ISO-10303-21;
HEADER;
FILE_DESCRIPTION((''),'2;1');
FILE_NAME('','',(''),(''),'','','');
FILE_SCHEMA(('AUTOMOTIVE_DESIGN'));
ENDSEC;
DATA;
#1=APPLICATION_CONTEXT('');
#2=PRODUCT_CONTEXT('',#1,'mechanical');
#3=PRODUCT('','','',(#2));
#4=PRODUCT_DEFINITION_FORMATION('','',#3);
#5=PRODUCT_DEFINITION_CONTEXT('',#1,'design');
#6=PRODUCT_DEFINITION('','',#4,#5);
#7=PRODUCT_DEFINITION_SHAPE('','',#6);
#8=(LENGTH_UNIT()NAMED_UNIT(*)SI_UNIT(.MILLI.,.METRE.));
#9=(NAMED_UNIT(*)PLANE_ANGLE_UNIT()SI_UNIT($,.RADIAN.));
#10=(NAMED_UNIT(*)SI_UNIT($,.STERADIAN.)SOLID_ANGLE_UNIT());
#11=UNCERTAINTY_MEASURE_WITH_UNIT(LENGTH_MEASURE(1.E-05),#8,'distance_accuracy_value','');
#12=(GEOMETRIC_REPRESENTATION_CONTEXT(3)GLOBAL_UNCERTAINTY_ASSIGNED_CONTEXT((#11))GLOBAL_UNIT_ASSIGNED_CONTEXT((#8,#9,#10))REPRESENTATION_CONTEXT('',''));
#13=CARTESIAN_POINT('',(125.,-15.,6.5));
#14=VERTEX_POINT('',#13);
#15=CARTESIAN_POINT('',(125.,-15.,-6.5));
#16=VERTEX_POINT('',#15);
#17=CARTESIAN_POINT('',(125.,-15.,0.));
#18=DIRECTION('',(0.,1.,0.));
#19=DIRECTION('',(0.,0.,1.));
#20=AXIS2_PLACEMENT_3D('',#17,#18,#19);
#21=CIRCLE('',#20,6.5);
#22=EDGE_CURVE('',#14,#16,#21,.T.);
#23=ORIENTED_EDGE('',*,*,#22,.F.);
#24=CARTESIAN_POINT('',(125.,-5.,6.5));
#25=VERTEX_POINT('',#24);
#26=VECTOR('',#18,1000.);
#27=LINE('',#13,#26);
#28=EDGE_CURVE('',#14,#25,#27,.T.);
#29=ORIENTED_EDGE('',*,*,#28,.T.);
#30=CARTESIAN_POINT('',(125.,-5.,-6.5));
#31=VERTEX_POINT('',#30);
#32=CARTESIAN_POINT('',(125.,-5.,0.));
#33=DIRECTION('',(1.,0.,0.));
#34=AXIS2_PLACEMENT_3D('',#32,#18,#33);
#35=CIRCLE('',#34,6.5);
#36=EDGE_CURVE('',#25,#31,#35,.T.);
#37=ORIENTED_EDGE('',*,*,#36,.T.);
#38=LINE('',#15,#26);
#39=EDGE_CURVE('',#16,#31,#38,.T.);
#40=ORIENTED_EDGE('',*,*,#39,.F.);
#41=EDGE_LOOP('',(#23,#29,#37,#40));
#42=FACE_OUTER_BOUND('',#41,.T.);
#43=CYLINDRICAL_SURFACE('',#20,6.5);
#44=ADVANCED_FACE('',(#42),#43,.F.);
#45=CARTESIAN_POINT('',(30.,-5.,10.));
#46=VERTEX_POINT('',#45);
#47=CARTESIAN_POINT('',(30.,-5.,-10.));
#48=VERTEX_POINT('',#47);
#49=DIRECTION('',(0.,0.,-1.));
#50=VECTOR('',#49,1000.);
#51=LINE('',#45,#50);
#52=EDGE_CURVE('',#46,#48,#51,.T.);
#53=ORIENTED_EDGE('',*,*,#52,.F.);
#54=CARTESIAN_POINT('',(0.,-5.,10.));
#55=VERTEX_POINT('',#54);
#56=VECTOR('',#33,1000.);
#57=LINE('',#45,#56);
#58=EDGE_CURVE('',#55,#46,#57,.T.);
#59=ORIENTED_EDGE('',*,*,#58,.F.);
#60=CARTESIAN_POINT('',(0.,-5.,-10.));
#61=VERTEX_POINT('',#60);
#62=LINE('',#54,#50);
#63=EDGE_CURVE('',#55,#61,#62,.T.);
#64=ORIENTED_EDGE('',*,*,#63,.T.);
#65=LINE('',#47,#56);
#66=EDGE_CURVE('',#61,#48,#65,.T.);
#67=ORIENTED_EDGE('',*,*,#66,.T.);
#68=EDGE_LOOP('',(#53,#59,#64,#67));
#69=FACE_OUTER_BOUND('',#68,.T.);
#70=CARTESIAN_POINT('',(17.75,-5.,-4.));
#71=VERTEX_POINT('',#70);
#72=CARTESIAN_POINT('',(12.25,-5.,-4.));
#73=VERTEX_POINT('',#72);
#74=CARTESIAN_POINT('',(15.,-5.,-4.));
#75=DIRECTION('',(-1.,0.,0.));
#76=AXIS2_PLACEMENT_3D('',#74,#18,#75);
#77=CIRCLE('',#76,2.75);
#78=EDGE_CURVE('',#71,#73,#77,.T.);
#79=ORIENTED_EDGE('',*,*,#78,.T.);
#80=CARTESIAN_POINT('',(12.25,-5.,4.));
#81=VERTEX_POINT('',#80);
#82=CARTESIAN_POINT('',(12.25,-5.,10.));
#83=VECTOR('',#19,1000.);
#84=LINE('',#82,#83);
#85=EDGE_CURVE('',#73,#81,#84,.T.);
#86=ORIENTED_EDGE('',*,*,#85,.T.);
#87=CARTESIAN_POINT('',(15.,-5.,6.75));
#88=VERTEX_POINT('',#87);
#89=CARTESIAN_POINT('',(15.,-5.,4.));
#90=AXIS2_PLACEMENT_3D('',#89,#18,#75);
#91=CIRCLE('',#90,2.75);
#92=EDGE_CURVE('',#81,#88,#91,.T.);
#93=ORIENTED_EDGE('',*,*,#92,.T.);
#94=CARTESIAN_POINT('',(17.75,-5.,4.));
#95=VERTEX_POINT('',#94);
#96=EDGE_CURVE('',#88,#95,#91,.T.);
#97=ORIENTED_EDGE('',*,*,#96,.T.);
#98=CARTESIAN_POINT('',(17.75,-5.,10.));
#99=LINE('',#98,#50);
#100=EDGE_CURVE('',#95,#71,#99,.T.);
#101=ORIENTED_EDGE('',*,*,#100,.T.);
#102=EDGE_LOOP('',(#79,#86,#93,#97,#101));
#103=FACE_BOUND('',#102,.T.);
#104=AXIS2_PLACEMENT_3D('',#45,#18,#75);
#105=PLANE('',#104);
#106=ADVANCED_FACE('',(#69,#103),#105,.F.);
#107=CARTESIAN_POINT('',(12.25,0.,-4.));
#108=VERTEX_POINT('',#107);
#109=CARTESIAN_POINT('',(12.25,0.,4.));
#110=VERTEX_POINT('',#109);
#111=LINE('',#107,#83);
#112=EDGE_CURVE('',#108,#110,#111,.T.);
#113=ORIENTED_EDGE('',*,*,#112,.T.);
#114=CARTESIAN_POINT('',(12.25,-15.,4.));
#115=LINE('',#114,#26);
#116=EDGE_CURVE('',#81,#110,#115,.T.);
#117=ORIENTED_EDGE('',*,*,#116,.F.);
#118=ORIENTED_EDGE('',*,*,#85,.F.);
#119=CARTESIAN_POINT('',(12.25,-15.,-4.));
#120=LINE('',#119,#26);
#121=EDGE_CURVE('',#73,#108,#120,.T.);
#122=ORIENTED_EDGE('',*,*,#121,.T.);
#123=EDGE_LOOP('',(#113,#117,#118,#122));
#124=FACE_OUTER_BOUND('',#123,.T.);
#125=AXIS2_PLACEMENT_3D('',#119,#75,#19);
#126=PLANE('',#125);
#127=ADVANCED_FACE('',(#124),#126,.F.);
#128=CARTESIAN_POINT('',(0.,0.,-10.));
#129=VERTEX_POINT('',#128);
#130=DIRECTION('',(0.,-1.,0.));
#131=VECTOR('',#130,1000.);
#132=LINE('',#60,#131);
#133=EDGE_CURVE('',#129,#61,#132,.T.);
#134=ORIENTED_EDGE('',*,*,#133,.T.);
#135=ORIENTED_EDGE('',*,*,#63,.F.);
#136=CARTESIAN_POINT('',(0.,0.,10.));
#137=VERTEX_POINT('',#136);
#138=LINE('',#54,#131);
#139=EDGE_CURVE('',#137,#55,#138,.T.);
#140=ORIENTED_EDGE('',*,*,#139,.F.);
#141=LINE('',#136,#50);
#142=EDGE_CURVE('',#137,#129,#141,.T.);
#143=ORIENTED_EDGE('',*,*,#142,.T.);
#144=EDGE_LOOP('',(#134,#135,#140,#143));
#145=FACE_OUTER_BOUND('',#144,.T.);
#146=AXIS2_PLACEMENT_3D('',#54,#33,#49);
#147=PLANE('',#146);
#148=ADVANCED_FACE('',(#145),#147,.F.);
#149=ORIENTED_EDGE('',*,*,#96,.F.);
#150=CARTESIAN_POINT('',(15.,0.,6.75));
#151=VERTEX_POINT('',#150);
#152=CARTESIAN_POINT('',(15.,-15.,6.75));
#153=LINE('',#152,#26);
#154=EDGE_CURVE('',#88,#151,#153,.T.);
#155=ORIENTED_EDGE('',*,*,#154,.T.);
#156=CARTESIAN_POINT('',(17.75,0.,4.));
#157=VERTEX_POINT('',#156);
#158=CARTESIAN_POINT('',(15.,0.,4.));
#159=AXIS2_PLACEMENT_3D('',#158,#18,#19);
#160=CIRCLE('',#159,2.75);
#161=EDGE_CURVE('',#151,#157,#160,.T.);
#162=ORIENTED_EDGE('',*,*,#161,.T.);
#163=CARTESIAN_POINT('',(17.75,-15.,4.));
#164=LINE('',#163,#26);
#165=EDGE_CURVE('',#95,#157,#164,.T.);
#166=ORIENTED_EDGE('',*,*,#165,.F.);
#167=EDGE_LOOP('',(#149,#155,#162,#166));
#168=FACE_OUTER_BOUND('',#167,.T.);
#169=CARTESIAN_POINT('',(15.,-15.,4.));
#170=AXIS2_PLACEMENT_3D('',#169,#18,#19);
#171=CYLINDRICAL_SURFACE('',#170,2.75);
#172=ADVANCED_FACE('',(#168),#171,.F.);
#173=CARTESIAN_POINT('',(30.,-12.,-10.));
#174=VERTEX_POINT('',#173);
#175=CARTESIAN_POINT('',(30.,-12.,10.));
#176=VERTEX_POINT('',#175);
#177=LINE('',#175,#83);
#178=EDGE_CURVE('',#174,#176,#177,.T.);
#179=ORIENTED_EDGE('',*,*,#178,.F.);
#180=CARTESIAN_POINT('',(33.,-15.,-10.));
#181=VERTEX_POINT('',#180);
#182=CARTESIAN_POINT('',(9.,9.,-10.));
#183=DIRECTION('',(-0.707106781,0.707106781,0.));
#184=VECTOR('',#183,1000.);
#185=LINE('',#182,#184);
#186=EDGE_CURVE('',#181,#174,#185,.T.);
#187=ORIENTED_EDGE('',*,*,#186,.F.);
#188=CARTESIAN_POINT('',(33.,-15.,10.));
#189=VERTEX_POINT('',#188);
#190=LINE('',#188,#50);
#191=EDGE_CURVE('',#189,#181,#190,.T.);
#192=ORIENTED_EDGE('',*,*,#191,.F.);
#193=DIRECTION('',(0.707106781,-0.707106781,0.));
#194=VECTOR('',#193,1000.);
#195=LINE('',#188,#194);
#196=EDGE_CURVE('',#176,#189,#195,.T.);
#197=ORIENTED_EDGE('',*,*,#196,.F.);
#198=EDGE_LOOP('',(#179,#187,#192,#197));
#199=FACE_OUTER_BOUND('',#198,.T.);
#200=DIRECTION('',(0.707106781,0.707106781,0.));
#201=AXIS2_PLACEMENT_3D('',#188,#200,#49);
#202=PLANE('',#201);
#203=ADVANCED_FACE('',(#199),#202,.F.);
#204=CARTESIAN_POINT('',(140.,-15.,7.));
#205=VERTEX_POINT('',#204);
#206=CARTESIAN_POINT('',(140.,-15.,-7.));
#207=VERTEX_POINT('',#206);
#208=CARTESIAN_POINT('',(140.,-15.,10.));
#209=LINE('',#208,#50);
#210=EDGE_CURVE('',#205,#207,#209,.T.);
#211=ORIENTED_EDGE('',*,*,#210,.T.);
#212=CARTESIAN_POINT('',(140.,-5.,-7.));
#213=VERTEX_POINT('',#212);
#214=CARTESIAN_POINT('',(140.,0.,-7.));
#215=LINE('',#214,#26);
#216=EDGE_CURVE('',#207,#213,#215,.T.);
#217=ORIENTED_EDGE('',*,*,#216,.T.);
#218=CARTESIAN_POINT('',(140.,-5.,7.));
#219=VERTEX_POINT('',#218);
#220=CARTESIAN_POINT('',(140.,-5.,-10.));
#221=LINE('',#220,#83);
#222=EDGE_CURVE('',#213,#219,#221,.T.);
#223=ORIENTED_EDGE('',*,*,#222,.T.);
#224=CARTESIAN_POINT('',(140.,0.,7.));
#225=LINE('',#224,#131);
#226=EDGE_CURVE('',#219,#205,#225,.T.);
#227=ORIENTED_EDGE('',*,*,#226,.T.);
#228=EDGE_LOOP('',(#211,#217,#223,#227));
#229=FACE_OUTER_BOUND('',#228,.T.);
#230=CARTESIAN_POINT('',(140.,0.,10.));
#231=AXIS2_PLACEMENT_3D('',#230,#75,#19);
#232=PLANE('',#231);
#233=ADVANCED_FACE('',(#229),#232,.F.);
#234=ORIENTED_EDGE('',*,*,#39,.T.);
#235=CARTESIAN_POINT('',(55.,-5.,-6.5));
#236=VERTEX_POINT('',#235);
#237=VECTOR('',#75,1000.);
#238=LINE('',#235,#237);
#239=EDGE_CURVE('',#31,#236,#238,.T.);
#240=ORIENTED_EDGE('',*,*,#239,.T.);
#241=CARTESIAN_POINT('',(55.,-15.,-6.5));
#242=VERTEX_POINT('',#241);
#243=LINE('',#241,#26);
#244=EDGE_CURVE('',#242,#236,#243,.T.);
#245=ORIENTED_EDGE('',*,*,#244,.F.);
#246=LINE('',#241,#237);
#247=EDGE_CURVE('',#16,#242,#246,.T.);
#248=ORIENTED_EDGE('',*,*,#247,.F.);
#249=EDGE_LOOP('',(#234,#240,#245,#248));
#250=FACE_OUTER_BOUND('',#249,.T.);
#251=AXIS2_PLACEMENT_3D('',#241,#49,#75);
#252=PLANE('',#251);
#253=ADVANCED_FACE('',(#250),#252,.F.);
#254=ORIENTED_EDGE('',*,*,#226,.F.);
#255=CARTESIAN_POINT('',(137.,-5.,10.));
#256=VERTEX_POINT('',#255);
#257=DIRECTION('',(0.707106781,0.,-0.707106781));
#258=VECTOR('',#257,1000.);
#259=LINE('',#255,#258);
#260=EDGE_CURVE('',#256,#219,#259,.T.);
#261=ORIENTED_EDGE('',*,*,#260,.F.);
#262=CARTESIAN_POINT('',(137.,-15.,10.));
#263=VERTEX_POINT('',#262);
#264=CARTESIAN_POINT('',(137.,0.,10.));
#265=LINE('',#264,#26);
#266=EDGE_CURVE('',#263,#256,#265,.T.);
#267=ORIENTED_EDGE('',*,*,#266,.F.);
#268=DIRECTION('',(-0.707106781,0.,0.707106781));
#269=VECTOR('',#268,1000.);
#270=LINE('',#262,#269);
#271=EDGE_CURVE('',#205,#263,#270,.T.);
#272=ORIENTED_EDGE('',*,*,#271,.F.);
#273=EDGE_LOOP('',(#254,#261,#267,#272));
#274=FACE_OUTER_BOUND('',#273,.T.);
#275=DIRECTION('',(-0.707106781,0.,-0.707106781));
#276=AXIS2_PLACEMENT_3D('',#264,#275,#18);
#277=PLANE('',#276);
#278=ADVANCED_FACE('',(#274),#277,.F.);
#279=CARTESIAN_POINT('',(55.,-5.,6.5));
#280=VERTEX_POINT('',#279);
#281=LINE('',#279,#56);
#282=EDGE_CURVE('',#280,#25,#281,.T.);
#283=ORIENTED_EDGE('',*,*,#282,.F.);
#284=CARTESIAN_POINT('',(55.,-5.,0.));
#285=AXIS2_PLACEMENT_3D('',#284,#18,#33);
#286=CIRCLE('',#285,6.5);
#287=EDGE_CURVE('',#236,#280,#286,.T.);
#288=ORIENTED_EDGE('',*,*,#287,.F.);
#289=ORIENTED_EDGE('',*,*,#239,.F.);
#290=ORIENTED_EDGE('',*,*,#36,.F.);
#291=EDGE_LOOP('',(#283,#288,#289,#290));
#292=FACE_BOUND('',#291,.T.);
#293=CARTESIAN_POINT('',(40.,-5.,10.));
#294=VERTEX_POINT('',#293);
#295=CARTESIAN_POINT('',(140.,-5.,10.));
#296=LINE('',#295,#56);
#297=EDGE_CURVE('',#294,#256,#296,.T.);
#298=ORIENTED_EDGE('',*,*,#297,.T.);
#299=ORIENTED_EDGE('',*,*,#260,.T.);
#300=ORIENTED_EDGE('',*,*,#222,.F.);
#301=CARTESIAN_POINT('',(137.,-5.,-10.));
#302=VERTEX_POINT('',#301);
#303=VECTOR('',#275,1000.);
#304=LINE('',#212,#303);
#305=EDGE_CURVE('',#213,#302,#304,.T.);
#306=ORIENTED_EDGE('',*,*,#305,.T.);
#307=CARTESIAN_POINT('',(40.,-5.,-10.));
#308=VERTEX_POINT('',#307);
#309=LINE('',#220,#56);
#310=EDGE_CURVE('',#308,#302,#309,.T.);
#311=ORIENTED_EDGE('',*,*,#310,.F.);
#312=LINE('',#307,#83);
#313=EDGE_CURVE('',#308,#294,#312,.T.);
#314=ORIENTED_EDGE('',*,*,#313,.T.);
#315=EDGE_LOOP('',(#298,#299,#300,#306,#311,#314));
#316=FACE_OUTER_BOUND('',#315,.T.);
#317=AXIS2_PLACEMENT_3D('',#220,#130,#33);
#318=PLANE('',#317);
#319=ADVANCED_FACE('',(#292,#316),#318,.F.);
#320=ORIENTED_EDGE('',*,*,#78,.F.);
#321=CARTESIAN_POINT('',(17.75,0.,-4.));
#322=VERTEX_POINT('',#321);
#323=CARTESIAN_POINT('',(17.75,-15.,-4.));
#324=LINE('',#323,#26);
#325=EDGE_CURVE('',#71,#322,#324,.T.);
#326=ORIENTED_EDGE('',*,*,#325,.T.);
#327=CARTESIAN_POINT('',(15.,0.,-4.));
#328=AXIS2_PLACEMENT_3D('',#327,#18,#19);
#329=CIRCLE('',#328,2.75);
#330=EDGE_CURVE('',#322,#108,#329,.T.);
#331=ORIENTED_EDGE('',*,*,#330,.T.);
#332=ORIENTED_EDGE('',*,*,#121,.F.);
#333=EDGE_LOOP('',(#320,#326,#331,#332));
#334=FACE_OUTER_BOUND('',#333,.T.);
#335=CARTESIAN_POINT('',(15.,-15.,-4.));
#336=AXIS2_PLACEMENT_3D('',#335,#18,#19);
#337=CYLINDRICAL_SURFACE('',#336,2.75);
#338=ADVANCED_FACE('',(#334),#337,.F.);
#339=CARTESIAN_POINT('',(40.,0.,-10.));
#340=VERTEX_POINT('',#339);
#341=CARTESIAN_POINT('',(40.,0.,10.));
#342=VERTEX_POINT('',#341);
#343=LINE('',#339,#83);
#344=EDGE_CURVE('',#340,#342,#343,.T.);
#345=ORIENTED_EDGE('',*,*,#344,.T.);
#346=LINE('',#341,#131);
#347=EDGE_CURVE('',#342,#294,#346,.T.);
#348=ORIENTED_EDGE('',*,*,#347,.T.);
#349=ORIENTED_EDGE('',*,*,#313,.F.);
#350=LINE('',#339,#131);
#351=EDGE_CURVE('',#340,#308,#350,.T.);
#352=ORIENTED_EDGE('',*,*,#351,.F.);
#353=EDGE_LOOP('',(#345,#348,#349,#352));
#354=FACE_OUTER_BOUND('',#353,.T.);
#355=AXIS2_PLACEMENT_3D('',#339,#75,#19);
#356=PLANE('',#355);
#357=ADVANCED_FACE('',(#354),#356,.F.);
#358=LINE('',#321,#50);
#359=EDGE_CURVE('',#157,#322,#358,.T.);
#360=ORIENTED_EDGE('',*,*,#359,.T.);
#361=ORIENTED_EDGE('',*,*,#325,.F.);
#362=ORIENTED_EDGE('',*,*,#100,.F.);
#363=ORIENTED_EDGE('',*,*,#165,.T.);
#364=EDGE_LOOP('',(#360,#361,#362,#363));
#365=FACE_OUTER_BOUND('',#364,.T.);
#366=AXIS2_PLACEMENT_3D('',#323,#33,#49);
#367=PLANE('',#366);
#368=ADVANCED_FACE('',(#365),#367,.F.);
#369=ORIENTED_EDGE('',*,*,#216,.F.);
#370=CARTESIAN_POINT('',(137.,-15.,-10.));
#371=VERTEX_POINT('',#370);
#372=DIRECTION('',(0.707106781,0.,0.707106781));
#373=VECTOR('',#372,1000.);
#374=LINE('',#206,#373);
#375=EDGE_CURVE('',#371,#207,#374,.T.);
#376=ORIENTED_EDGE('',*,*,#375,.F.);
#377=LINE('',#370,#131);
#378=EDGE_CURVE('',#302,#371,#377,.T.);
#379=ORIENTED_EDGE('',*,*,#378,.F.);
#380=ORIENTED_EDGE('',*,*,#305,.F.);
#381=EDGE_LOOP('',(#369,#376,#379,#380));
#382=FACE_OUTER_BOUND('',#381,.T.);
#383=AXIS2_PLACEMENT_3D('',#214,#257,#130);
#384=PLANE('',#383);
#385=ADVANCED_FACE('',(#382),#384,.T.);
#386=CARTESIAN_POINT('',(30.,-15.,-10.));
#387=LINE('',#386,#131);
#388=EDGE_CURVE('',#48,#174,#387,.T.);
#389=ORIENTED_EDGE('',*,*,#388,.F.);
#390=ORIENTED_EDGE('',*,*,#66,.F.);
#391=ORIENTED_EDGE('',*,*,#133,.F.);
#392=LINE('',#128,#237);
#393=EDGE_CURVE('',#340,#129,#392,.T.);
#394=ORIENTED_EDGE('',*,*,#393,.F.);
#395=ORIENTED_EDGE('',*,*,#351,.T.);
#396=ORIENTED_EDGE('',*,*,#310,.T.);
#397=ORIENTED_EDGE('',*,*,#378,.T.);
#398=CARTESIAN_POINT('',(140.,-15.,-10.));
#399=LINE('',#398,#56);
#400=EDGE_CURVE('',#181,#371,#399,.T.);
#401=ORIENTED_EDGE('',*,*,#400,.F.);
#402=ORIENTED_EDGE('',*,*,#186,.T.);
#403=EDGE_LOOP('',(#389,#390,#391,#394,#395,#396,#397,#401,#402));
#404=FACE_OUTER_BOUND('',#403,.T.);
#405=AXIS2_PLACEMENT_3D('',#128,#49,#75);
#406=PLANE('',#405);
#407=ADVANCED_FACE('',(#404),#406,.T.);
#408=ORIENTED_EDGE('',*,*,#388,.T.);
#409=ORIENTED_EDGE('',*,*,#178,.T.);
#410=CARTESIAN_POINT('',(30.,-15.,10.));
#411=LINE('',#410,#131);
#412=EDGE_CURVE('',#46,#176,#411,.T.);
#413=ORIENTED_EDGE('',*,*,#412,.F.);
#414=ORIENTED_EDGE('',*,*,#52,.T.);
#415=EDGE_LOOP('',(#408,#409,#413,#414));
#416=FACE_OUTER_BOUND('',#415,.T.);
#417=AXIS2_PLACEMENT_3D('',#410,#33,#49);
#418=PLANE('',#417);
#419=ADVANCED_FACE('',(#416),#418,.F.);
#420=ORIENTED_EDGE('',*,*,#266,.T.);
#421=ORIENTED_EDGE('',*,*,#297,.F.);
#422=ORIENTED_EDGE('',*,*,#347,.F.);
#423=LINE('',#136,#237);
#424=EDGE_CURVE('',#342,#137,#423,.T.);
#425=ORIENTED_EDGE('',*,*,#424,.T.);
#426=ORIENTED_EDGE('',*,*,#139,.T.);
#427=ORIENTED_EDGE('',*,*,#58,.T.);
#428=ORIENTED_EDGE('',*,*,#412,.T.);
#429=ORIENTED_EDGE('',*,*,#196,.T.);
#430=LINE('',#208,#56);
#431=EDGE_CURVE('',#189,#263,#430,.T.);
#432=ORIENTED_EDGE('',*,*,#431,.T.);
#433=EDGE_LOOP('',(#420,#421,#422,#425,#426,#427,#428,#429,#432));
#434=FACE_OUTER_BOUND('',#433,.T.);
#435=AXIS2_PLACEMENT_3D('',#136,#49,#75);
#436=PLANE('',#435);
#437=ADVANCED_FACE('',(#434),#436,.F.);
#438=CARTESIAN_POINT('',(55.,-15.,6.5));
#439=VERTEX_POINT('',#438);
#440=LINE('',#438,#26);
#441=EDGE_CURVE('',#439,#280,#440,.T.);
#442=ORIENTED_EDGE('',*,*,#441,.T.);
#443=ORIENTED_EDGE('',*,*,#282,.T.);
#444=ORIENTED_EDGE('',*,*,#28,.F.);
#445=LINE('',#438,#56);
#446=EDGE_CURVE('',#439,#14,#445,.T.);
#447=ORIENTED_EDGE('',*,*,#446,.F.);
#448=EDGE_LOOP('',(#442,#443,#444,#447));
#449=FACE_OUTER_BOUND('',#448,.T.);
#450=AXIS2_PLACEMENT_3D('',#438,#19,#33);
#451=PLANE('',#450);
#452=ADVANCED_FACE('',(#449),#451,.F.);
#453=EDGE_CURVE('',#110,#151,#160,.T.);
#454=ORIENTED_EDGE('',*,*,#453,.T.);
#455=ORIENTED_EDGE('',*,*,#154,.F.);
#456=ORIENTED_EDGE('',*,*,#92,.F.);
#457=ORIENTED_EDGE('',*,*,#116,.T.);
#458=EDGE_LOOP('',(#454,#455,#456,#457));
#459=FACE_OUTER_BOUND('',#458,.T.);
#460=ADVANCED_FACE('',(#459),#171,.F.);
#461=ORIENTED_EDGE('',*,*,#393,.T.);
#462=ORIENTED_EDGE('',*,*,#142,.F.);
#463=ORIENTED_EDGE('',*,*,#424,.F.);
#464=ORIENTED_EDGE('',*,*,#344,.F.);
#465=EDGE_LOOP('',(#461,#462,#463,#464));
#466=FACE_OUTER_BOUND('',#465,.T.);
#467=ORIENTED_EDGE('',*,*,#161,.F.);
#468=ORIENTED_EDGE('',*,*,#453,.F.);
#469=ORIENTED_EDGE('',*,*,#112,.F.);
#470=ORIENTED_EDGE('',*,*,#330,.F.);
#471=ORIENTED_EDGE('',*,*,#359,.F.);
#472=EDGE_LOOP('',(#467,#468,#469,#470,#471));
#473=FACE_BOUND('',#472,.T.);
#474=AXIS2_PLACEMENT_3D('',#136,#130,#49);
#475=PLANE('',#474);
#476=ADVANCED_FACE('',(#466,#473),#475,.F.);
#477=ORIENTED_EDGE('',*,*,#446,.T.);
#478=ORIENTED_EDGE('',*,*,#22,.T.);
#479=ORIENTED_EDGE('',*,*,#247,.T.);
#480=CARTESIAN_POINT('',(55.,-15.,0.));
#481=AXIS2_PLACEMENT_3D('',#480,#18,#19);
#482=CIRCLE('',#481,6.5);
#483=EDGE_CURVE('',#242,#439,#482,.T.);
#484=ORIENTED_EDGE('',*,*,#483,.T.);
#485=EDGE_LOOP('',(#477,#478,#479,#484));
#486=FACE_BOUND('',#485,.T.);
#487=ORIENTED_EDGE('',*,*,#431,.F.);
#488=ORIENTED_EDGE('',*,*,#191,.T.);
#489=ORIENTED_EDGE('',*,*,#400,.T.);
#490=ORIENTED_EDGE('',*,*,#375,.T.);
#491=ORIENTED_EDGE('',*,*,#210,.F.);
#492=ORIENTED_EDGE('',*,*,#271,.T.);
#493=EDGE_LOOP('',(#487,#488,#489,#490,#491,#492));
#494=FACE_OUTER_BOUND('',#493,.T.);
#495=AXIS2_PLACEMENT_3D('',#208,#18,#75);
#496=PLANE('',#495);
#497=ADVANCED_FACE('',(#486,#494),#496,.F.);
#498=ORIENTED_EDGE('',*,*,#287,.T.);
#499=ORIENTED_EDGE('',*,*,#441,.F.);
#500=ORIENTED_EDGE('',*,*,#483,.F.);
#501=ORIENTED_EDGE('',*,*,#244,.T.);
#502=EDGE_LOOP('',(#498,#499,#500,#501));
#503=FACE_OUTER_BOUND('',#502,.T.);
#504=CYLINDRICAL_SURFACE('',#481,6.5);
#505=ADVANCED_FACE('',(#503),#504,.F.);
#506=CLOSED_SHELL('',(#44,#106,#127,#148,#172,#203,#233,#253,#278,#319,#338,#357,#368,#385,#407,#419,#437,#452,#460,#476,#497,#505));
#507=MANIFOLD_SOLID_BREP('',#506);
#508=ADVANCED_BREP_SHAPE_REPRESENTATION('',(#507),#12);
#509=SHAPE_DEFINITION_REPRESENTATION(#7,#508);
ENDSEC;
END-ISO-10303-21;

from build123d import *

# Parameters (mm, degrees)
EXTRUDE_1_DEPTH     = 10
CUT_EXTRUDE_1_DEPTH = 142.155942135
CUT_EXTRUDE_2_DEPTH = 142.155942135
CHAMFER_1_SIZE      = 3
CHAMFER_2_SIZE      = 3
SKETCH_5_W          = 100
SKETCH_5_H          = 5
CUT_EXTRUDE_3_DEPTH = 143.214626533


with BuildPart() as part:
    # 草图2 → 凸台-拉伸1 (new, symmetric)
    with BuildSketch(Plane.XY):
        Polygon((0, 0), (140, 0), (140, -15), (30, -15), (30, -5), (0, -5), align=None)
    extrude(amount=EXTRUDE_1_DEPTH, both=True)

    # 草图3 → 切除-拉伸1 (cut, through all)
    with BuildSketch(Plane(origin=(0, 0, 0), x_dir=(1, 0, 0), z_dir=(0, 1, 0))):
        with BuildLine():
            Line((55, 6.5), (125, 6.5))
            ThreePointArc((125, 6.5), (131.5, 0), (125, -6.5))
            Line((125, -6.5), (55, -6.5))
            ThreePointArc((55, -6.5), (48.5, 0), (55, 6.5))
        make_face()
    extrude(amount=-CUT_EXTRUDE_1_DEPTH, mode=Mode.SUBTRACT)

    # 草图4 → 切除-拉伸2 (cut, through all)
    with BuildSketch(Plane(origin=(0, 0, 0), x_dir=(1, 0, 0), z_dir=(0, 1, 0))):
        with BuildLine():
            Line((17.75, 4), (17.75, -4))
            ThreePointArc((17.75, -4), (15, -6.75), (12.25, -4))
            Line((12.25, -4), (12.25, 4))
            ThreePointArc((12.25, 4), (15, 6.75), (17.75, 4))
        make_face()
    extrude(amount=-CUT_EXTRUDE_2_DEPTH, mode=Mode.SUBTRACT)

    # 倒角1
    chamfer_1_edges = [part.edges().sort_by_distance(p)[0] for p in [
        (140, -7.5, 10),
        (140, -7.5, -10),
    ]]
    chamfer(chamfer_1_edges, length=CHAMFER_1_SIZE)

    # 倒角2
    chamfer_2_edges = [part.edges().sort_by_distance(p)[0] for p in [
        (30, -15, 0),
    ]]
    chamfer(chamfer_2_edges, length=CHAMFER_2_SIZE)

    # 草图5 → 切除-拉伸3 (cut, through all)
    with BuildSketch(Plane.XY.offset(10)):
        with Locations((90, -2.5)):
            Rectangle(SKETCH_5_W, SKETCH_5_H)
    extrude(amount=-CUT_EXTRUDE_3_DEPTH, mode=Mode.SUBTRACT)


solid = part.part
